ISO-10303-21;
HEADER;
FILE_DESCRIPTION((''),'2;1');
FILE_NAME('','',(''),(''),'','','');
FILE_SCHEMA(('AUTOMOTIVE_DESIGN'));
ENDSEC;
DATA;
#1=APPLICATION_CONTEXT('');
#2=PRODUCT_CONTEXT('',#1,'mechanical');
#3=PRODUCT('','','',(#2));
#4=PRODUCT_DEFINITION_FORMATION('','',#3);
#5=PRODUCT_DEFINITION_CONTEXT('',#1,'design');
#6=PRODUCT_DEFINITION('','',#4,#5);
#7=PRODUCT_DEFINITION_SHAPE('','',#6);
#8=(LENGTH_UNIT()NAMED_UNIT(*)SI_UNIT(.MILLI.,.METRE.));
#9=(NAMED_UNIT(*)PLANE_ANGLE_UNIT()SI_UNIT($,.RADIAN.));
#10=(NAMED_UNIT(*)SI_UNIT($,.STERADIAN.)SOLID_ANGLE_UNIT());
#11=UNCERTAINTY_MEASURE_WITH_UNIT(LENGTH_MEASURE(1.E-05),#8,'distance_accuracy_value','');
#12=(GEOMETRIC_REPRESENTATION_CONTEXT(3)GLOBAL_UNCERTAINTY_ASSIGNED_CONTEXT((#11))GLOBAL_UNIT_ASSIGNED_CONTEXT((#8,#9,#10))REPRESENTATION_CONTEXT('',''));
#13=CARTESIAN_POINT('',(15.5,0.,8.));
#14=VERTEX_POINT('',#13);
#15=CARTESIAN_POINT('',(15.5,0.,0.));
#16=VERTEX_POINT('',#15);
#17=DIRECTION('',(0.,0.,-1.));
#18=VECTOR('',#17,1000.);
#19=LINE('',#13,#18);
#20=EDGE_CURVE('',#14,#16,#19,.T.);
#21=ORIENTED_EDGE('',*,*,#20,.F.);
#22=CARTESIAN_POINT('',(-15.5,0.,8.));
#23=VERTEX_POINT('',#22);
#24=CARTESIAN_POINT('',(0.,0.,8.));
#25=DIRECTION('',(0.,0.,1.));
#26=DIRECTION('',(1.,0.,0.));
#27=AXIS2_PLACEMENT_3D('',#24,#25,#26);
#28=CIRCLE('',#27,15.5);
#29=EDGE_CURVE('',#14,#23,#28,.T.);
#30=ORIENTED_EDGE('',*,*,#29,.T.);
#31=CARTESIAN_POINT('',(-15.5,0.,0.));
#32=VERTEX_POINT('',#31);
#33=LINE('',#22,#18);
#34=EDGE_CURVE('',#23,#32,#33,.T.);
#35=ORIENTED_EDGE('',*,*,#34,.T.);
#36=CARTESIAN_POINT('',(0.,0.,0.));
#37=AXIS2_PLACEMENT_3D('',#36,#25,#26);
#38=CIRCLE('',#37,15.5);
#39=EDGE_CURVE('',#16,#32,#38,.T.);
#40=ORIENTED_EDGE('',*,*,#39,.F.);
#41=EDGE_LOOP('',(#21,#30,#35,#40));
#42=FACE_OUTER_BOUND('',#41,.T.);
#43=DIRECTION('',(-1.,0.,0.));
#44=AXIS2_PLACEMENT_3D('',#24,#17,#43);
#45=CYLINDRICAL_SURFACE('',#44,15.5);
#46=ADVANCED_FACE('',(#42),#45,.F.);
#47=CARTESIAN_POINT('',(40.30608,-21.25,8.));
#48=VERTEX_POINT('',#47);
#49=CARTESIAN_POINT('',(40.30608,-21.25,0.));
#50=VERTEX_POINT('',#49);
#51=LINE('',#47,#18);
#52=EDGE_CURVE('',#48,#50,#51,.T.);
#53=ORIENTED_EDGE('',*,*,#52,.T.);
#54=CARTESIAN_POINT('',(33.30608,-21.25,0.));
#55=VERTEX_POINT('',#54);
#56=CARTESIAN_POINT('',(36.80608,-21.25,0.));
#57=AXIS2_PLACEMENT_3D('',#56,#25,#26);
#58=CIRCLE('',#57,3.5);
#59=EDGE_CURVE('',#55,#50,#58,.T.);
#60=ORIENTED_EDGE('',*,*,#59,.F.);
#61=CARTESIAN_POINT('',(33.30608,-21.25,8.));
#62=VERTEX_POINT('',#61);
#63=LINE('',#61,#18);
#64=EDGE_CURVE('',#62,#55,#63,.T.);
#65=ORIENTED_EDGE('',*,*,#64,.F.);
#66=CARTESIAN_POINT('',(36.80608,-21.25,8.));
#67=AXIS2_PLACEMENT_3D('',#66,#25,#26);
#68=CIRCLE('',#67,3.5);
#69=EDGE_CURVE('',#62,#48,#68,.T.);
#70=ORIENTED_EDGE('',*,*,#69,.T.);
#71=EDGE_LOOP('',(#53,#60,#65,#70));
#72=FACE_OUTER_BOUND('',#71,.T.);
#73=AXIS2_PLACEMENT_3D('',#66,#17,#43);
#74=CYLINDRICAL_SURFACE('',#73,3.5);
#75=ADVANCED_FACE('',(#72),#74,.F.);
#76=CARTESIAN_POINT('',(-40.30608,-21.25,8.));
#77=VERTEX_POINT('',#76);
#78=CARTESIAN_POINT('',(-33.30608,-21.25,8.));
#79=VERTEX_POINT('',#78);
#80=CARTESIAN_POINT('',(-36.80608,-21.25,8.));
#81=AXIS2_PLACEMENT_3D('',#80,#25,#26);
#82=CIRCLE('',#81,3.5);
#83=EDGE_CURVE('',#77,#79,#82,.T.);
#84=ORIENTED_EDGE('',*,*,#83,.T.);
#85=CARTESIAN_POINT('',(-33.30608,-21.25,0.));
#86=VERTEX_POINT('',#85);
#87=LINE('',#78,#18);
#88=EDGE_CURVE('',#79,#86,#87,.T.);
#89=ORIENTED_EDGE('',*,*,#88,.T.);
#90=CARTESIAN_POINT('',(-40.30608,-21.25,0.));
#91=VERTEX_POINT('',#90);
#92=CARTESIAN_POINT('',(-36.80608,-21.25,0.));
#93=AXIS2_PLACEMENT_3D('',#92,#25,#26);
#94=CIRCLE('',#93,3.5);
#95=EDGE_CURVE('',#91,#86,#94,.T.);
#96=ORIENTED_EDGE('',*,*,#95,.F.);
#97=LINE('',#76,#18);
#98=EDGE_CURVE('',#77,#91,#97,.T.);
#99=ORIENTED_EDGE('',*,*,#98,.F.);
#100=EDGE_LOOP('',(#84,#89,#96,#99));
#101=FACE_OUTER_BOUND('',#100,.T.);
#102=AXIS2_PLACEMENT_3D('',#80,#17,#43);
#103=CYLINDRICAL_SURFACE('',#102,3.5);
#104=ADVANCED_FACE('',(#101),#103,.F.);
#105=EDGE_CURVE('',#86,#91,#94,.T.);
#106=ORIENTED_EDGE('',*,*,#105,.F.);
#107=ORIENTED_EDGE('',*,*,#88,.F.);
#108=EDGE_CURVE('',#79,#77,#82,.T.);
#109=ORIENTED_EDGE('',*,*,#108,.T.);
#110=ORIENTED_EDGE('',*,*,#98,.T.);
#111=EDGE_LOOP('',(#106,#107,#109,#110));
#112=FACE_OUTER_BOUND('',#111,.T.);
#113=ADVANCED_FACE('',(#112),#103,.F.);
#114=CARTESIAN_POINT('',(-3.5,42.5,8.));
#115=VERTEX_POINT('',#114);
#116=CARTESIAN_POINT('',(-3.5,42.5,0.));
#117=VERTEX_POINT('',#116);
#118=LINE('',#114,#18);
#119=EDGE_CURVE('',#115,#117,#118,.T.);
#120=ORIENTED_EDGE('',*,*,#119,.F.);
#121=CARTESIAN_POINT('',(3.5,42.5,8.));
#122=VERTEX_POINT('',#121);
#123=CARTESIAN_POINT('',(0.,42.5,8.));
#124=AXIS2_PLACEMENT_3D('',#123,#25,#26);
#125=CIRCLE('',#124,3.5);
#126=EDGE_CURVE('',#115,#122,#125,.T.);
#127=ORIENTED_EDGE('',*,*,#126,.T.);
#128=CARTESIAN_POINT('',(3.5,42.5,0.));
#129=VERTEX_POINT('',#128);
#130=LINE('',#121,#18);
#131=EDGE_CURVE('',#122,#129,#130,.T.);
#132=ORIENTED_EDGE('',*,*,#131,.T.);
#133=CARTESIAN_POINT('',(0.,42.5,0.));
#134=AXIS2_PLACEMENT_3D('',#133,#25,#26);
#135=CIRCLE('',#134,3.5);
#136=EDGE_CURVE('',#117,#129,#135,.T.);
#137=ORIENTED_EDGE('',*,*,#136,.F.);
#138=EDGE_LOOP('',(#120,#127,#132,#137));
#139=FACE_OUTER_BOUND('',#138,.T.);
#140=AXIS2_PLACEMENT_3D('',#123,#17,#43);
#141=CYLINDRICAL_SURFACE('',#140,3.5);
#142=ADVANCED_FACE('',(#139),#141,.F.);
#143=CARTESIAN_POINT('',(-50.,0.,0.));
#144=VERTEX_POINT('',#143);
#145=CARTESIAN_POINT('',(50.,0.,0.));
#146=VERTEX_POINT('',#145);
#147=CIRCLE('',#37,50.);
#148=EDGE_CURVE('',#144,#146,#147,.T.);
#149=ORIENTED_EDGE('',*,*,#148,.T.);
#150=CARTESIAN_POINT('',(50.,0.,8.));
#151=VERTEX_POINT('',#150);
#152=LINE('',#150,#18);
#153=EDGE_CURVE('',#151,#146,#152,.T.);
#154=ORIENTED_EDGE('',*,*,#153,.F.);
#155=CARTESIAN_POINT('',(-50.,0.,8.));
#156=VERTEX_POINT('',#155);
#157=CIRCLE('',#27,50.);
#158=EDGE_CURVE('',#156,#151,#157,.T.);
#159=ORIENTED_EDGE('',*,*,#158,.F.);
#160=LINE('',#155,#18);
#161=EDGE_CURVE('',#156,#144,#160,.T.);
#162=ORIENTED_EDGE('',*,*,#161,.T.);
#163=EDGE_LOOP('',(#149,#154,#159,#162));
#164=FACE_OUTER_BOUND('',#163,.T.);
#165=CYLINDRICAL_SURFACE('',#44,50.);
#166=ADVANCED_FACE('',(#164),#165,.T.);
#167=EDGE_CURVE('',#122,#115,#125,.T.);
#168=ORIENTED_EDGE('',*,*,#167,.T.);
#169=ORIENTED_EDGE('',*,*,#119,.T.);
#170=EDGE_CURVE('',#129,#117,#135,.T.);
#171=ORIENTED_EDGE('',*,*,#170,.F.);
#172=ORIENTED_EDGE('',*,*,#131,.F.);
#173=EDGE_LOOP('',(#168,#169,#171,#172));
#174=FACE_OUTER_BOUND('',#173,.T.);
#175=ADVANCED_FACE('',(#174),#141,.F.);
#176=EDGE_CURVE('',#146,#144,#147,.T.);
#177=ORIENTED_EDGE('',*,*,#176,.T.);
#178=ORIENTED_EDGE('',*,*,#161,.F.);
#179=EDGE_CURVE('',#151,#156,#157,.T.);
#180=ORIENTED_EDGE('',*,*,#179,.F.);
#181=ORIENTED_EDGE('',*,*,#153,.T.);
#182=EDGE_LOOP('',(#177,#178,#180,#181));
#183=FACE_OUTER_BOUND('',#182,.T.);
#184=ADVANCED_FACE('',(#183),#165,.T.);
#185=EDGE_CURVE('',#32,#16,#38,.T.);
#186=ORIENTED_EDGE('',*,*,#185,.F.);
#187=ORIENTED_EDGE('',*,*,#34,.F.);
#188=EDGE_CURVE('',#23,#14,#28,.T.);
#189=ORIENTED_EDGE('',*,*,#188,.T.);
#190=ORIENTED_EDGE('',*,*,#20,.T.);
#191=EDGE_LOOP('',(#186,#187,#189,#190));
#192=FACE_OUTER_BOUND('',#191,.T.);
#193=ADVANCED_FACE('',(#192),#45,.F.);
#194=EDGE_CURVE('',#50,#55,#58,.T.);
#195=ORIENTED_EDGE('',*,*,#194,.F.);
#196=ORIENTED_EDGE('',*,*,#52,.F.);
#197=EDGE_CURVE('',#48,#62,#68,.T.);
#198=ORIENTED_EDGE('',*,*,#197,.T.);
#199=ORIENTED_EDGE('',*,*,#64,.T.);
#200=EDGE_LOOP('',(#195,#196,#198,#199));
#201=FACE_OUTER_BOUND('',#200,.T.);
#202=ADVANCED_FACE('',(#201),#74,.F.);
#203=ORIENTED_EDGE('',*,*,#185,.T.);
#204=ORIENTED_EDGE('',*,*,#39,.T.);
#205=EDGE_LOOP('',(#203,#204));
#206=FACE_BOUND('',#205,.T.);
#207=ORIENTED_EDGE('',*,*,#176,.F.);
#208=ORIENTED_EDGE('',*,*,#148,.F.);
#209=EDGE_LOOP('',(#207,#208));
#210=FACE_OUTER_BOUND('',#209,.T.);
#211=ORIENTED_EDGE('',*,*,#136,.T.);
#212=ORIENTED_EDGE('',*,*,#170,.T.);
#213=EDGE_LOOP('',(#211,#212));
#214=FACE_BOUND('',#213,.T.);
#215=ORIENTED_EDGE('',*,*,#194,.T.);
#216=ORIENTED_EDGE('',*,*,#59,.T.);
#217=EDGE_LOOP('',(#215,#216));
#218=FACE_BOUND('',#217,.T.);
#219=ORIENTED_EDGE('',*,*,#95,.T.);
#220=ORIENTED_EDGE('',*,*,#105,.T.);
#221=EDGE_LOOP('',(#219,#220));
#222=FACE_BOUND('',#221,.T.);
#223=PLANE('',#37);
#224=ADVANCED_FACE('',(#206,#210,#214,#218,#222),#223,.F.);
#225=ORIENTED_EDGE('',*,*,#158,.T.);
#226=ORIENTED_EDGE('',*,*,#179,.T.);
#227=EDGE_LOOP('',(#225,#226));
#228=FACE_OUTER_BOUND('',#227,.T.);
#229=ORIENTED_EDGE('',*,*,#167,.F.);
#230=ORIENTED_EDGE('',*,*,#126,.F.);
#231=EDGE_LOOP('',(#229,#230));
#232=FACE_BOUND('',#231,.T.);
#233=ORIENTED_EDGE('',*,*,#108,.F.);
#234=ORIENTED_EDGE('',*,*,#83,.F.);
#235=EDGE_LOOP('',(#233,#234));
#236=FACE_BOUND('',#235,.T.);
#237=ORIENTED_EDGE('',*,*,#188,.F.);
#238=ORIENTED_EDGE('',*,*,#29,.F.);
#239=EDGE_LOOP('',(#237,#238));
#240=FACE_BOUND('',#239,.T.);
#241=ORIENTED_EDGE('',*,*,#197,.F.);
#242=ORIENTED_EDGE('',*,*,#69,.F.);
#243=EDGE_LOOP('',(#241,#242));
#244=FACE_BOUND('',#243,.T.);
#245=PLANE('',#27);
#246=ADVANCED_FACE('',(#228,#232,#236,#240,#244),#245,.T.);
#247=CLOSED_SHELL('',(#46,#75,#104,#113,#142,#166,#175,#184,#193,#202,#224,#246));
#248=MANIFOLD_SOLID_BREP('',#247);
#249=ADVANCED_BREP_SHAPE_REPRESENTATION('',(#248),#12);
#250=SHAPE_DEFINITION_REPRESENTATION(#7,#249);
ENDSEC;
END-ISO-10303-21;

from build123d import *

# Parameters (mm, degrees)
SKETCH1_R           = 50
SKETCH1_R_2         = 3.5
SKETCH1_R_3         = 15.5
BOSS_EXTRUDE1_DEPTH = 8


with BuildPart() as part:
    # Sketch1 → Boss-Extrude1 (new body)
    with BuildSketch(Plane.XY):
        Circle(SKETCH1_R)
        with Locations((0, 42.5)):
            Circle(SKETCH1_R_2, mode=Mode.SUBTRACT)
        with Locations((-36.806079661, -21.25)):
            Circle(SKETCH1_R_2, mode=Mode.SUBTRACT)
        with Locations((36.806079661, -21.25)):
            Circle(SKETCH1_R_2, mode=Mode.SUBTRACT)
        Circle(SKETCH1_R_3, mode=Mode.SUBTRACT)
    extrude(amount=BOSS_EXTRUDE1_DEPTH)


solid = part.part
